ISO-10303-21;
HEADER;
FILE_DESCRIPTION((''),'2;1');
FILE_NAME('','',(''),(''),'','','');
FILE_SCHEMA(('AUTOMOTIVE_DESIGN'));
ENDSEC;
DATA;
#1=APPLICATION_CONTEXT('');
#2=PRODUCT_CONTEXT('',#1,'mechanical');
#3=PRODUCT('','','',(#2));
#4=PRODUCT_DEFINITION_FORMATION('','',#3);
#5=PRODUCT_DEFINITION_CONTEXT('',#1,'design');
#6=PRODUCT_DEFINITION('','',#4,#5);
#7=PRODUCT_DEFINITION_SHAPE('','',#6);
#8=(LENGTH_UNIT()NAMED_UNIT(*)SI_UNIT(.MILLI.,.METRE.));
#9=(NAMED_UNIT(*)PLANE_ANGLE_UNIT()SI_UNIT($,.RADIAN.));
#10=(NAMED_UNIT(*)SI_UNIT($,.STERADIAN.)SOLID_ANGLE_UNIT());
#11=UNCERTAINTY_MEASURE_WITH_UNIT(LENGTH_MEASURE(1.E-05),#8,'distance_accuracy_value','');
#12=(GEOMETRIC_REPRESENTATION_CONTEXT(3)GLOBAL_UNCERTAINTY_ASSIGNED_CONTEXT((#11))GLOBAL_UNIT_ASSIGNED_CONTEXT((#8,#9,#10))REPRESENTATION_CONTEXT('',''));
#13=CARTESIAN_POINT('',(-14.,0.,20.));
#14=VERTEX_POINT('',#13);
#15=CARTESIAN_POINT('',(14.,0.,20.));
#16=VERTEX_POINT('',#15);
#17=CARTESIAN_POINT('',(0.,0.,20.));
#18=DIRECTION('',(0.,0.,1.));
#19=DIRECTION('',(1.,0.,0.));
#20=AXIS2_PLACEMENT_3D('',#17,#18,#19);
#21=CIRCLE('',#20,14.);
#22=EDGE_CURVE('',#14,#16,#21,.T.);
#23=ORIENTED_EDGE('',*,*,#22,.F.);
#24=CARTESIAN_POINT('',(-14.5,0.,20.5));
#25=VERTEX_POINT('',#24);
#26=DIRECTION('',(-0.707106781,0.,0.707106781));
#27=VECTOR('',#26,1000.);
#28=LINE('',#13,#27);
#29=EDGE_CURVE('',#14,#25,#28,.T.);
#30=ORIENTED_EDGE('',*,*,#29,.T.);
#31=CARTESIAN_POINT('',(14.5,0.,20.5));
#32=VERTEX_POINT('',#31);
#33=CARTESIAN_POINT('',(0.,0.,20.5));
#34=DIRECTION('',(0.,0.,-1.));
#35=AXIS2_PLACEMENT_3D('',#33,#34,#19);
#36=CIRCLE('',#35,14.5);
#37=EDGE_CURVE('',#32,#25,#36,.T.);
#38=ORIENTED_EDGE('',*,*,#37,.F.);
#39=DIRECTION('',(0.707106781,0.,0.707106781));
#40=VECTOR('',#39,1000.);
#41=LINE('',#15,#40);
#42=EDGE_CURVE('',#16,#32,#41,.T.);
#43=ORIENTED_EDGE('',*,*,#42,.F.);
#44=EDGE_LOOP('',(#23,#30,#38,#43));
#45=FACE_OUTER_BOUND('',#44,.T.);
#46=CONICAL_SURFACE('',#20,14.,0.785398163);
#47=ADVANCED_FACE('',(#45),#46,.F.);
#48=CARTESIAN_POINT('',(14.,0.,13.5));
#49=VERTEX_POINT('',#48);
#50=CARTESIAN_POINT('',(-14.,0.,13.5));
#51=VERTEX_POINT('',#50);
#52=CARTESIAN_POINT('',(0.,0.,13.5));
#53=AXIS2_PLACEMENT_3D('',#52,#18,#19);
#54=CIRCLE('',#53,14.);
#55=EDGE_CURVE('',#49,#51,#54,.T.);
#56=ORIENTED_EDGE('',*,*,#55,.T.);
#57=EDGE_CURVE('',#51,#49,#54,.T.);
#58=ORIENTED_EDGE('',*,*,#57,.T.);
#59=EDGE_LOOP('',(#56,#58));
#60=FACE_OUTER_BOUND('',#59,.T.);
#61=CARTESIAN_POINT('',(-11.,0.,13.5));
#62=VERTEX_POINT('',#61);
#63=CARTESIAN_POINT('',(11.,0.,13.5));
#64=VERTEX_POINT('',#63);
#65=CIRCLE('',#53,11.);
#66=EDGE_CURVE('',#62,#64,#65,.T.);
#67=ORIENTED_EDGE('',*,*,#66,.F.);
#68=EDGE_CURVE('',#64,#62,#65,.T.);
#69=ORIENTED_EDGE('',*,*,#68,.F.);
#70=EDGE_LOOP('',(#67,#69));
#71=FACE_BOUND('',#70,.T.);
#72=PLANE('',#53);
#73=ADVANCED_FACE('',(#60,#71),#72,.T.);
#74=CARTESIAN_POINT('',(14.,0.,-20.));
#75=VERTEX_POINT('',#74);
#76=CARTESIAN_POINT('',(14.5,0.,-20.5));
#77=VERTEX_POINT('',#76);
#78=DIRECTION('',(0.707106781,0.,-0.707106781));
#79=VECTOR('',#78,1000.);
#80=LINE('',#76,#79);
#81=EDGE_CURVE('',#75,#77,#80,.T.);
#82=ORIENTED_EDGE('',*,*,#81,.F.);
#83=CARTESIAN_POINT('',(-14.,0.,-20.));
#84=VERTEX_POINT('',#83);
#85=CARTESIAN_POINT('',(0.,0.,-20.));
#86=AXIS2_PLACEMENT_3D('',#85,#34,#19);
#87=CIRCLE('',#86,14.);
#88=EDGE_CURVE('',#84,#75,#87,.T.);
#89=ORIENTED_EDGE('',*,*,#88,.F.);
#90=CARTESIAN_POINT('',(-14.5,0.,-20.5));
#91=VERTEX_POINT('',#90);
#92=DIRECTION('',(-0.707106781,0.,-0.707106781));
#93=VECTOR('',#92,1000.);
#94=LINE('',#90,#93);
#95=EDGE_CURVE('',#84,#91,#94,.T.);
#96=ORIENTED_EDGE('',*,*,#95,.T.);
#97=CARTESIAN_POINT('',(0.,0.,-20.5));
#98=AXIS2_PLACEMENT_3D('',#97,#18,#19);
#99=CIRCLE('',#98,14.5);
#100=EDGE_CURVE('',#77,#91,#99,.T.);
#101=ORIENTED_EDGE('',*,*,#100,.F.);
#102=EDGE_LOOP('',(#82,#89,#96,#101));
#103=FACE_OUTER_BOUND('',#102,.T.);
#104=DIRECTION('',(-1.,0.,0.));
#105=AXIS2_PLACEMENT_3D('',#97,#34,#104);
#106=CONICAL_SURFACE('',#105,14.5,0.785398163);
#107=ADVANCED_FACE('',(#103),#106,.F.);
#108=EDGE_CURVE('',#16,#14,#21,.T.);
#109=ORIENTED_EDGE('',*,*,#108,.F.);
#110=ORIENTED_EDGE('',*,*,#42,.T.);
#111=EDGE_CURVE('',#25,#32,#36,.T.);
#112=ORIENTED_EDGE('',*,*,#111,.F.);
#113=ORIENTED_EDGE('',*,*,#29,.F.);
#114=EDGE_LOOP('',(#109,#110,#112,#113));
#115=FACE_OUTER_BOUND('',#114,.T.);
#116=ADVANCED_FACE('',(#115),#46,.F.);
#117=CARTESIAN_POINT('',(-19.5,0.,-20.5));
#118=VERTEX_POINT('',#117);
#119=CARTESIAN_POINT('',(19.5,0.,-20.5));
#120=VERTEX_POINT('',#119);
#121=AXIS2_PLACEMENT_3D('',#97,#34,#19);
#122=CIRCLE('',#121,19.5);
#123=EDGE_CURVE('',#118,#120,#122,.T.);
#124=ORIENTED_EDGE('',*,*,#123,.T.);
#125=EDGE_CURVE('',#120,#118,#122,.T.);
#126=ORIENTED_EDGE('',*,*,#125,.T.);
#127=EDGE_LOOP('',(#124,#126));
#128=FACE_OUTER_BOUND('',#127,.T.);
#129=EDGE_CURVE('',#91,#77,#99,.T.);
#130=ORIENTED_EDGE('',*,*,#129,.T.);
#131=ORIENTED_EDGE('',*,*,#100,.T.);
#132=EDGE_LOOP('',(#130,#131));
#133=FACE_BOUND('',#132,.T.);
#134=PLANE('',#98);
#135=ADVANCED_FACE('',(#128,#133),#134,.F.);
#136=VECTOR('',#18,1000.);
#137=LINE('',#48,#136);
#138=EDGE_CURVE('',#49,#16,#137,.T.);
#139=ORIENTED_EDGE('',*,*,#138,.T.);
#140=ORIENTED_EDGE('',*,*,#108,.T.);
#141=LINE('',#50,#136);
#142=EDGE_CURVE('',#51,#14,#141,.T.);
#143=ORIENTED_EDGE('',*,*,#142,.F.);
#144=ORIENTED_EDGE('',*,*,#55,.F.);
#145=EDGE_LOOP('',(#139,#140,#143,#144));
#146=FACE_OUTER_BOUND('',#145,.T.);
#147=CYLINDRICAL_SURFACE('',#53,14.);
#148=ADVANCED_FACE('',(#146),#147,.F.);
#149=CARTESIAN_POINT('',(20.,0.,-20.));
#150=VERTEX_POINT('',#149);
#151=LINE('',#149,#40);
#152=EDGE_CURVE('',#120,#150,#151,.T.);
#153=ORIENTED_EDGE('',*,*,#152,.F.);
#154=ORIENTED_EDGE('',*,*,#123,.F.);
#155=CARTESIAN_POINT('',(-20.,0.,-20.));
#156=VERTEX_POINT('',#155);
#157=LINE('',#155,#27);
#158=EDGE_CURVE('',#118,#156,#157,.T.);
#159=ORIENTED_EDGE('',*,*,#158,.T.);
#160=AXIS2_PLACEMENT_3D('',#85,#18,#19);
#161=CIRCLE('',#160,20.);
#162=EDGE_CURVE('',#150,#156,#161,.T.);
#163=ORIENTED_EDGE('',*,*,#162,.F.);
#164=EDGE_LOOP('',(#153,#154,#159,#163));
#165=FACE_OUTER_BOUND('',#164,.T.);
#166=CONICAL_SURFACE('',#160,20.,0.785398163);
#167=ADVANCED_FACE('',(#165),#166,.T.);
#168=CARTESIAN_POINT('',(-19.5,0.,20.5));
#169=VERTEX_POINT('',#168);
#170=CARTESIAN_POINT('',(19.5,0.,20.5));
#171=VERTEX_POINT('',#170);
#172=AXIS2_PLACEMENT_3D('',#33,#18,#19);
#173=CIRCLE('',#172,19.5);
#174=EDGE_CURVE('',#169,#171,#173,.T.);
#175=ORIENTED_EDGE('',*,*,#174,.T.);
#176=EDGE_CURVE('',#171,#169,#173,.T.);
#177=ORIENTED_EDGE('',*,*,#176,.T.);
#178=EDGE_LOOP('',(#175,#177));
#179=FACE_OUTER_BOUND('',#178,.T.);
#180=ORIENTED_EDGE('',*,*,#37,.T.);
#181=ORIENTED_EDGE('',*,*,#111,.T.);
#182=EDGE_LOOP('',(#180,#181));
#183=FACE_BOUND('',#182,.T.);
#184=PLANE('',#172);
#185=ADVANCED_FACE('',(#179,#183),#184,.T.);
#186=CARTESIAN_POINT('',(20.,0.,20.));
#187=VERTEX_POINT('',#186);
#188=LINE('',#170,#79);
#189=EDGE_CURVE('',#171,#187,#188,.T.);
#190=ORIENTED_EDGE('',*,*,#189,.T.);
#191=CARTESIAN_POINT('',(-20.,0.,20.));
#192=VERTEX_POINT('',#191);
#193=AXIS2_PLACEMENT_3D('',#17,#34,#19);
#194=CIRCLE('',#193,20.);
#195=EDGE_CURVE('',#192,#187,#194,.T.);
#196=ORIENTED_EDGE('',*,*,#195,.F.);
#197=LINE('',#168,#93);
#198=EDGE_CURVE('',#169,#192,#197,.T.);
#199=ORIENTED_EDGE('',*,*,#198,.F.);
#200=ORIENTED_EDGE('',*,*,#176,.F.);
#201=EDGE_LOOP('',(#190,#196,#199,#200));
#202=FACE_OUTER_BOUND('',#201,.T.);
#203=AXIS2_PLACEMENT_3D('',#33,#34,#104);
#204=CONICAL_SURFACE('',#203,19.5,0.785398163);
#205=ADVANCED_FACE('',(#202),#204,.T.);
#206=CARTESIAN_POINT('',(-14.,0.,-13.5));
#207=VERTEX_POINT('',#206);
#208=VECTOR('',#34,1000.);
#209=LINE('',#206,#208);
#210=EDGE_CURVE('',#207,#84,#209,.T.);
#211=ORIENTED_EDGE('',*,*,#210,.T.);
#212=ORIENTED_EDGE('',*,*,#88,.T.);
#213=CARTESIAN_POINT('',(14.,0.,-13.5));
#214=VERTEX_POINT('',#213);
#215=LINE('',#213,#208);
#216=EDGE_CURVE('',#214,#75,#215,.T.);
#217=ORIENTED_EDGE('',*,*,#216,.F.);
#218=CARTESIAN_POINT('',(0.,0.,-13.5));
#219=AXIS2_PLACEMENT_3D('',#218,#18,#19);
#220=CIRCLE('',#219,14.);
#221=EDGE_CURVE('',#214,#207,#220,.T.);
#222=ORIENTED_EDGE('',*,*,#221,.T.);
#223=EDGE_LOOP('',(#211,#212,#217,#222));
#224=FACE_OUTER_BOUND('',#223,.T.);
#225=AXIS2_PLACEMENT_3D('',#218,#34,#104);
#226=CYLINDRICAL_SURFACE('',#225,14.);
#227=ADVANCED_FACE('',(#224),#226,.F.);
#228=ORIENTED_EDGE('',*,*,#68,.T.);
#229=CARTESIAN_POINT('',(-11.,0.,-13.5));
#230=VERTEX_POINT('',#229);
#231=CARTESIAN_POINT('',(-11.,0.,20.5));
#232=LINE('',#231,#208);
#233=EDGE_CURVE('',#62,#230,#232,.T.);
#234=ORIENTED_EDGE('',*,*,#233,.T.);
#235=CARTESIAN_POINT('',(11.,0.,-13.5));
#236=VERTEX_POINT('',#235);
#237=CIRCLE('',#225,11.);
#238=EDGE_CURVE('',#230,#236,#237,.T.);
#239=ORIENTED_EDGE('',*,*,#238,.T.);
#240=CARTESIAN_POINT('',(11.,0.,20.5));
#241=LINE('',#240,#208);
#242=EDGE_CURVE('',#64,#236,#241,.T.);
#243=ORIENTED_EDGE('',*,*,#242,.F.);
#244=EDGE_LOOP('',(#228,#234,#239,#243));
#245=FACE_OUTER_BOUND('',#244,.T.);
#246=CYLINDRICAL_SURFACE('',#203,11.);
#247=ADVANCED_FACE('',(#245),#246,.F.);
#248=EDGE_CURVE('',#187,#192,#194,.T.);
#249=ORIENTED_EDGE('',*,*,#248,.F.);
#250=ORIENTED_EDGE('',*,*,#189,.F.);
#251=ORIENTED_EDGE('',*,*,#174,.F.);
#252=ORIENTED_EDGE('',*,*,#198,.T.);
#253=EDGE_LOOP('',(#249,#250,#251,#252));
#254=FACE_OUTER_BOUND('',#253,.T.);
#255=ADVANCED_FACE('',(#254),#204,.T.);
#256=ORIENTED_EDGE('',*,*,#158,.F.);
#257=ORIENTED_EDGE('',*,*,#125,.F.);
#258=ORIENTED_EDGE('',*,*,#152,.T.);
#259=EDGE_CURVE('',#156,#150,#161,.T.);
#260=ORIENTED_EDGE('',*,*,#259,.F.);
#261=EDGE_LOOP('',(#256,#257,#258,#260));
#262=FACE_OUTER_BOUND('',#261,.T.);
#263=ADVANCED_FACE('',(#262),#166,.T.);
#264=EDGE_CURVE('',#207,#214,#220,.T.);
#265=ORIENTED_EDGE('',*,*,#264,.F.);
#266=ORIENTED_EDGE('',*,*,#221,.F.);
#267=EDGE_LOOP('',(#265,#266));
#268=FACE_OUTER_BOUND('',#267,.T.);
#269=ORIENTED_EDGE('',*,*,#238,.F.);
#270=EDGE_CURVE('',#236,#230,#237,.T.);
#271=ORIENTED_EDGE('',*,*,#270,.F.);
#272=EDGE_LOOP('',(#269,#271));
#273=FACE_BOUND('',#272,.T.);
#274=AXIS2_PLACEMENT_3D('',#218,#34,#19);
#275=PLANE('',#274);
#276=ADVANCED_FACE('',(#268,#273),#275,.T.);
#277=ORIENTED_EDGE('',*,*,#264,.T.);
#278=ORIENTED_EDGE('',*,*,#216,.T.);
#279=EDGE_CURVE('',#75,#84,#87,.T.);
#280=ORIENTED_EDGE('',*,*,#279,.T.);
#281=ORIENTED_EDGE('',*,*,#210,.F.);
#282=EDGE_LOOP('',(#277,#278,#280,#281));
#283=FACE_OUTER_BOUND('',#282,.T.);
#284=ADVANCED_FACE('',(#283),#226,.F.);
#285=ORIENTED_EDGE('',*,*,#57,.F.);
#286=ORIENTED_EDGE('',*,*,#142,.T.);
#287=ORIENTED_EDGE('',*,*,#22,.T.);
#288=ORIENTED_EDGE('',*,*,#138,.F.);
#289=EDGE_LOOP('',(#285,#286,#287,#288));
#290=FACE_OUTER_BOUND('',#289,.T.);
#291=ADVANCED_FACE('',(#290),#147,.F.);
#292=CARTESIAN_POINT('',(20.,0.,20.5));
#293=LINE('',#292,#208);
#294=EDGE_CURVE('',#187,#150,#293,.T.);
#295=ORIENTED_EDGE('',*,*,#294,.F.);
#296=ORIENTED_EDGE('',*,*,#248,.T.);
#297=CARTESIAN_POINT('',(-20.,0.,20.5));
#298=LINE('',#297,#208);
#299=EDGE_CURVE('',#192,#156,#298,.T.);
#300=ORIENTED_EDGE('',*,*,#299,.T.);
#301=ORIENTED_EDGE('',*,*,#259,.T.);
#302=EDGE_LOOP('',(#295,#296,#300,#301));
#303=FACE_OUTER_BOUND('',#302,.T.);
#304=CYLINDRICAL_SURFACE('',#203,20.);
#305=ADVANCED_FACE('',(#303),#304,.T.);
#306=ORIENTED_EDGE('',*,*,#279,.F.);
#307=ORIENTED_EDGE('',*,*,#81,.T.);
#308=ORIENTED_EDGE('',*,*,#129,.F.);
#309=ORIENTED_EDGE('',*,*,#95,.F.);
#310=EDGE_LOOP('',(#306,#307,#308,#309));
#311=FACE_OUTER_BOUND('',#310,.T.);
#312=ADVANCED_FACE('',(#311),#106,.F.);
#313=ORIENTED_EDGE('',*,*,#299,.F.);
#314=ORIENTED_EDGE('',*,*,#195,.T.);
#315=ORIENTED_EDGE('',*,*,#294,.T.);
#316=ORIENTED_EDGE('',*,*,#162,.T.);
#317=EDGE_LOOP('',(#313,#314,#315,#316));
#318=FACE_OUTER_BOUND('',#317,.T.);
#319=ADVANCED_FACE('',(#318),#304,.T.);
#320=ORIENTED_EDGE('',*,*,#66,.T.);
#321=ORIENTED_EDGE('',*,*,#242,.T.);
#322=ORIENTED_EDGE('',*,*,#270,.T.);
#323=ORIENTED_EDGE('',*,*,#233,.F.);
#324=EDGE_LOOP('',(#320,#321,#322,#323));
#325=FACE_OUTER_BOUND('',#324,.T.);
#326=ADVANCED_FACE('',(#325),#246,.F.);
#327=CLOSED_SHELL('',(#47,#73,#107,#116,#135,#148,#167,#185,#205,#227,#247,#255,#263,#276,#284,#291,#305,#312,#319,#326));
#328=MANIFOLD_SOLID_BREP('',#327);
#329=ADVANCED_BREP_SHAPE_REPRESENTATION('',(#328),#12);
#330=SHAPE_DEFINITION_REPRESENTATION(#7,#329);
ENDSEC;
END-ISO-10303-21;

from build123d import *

# Parameters (mm, degrees)
SKETCH_2_R          = 20
SKETCH_2_R_2        = 11
EXTRUDE_1_DEPTH     = 20.5
SKETCH_3_R          = 14
CUT_EXTRUDE_1_DEPTH = 7
CHAMFER_3_SIZE      = 0.5


with BuildPart() as part:
    # 草图2 → 凸台-拉伸1 (new, symmetric)
    with BuildSketch(Plane.XY):
        Circle(SKETCH_2_R)
        Circle(SKETCH_2_R_2, mode=Mode.SUBTRACT)
    extrude(amount=EXTRUDE_1_DEPTH, both=True)

    # 草图3 → 切除-拉伸1 (cut)
    with BuildSketch(Plane.XY.offset(20.5)):
        Circle(SKETCH_3_R)
    cut_extrude_1 = extrude(amount=-CUT_EXTRUDE_1_DEPTH, mode=Mode.SUBTRACT)

    # 镜向6: 切除-拉伸1 across plane
    add(cut_extrude_1.mirror(Plane.XY), mode=Mode.SUBTRACT)

    # 倒角3
    chamfer_3_edges = [part.edges().sort_by_distance(p)[0] for p in [
        (-14, 0, 20.5),
        (-14, 0, -20.5),
        (-20, 0, -20.5),
        (-20, 0, 20.5),
    ]]
    chamfer(chamfer_3_edges, length=CHAMFER_3_SIZE)


solid = part.part
